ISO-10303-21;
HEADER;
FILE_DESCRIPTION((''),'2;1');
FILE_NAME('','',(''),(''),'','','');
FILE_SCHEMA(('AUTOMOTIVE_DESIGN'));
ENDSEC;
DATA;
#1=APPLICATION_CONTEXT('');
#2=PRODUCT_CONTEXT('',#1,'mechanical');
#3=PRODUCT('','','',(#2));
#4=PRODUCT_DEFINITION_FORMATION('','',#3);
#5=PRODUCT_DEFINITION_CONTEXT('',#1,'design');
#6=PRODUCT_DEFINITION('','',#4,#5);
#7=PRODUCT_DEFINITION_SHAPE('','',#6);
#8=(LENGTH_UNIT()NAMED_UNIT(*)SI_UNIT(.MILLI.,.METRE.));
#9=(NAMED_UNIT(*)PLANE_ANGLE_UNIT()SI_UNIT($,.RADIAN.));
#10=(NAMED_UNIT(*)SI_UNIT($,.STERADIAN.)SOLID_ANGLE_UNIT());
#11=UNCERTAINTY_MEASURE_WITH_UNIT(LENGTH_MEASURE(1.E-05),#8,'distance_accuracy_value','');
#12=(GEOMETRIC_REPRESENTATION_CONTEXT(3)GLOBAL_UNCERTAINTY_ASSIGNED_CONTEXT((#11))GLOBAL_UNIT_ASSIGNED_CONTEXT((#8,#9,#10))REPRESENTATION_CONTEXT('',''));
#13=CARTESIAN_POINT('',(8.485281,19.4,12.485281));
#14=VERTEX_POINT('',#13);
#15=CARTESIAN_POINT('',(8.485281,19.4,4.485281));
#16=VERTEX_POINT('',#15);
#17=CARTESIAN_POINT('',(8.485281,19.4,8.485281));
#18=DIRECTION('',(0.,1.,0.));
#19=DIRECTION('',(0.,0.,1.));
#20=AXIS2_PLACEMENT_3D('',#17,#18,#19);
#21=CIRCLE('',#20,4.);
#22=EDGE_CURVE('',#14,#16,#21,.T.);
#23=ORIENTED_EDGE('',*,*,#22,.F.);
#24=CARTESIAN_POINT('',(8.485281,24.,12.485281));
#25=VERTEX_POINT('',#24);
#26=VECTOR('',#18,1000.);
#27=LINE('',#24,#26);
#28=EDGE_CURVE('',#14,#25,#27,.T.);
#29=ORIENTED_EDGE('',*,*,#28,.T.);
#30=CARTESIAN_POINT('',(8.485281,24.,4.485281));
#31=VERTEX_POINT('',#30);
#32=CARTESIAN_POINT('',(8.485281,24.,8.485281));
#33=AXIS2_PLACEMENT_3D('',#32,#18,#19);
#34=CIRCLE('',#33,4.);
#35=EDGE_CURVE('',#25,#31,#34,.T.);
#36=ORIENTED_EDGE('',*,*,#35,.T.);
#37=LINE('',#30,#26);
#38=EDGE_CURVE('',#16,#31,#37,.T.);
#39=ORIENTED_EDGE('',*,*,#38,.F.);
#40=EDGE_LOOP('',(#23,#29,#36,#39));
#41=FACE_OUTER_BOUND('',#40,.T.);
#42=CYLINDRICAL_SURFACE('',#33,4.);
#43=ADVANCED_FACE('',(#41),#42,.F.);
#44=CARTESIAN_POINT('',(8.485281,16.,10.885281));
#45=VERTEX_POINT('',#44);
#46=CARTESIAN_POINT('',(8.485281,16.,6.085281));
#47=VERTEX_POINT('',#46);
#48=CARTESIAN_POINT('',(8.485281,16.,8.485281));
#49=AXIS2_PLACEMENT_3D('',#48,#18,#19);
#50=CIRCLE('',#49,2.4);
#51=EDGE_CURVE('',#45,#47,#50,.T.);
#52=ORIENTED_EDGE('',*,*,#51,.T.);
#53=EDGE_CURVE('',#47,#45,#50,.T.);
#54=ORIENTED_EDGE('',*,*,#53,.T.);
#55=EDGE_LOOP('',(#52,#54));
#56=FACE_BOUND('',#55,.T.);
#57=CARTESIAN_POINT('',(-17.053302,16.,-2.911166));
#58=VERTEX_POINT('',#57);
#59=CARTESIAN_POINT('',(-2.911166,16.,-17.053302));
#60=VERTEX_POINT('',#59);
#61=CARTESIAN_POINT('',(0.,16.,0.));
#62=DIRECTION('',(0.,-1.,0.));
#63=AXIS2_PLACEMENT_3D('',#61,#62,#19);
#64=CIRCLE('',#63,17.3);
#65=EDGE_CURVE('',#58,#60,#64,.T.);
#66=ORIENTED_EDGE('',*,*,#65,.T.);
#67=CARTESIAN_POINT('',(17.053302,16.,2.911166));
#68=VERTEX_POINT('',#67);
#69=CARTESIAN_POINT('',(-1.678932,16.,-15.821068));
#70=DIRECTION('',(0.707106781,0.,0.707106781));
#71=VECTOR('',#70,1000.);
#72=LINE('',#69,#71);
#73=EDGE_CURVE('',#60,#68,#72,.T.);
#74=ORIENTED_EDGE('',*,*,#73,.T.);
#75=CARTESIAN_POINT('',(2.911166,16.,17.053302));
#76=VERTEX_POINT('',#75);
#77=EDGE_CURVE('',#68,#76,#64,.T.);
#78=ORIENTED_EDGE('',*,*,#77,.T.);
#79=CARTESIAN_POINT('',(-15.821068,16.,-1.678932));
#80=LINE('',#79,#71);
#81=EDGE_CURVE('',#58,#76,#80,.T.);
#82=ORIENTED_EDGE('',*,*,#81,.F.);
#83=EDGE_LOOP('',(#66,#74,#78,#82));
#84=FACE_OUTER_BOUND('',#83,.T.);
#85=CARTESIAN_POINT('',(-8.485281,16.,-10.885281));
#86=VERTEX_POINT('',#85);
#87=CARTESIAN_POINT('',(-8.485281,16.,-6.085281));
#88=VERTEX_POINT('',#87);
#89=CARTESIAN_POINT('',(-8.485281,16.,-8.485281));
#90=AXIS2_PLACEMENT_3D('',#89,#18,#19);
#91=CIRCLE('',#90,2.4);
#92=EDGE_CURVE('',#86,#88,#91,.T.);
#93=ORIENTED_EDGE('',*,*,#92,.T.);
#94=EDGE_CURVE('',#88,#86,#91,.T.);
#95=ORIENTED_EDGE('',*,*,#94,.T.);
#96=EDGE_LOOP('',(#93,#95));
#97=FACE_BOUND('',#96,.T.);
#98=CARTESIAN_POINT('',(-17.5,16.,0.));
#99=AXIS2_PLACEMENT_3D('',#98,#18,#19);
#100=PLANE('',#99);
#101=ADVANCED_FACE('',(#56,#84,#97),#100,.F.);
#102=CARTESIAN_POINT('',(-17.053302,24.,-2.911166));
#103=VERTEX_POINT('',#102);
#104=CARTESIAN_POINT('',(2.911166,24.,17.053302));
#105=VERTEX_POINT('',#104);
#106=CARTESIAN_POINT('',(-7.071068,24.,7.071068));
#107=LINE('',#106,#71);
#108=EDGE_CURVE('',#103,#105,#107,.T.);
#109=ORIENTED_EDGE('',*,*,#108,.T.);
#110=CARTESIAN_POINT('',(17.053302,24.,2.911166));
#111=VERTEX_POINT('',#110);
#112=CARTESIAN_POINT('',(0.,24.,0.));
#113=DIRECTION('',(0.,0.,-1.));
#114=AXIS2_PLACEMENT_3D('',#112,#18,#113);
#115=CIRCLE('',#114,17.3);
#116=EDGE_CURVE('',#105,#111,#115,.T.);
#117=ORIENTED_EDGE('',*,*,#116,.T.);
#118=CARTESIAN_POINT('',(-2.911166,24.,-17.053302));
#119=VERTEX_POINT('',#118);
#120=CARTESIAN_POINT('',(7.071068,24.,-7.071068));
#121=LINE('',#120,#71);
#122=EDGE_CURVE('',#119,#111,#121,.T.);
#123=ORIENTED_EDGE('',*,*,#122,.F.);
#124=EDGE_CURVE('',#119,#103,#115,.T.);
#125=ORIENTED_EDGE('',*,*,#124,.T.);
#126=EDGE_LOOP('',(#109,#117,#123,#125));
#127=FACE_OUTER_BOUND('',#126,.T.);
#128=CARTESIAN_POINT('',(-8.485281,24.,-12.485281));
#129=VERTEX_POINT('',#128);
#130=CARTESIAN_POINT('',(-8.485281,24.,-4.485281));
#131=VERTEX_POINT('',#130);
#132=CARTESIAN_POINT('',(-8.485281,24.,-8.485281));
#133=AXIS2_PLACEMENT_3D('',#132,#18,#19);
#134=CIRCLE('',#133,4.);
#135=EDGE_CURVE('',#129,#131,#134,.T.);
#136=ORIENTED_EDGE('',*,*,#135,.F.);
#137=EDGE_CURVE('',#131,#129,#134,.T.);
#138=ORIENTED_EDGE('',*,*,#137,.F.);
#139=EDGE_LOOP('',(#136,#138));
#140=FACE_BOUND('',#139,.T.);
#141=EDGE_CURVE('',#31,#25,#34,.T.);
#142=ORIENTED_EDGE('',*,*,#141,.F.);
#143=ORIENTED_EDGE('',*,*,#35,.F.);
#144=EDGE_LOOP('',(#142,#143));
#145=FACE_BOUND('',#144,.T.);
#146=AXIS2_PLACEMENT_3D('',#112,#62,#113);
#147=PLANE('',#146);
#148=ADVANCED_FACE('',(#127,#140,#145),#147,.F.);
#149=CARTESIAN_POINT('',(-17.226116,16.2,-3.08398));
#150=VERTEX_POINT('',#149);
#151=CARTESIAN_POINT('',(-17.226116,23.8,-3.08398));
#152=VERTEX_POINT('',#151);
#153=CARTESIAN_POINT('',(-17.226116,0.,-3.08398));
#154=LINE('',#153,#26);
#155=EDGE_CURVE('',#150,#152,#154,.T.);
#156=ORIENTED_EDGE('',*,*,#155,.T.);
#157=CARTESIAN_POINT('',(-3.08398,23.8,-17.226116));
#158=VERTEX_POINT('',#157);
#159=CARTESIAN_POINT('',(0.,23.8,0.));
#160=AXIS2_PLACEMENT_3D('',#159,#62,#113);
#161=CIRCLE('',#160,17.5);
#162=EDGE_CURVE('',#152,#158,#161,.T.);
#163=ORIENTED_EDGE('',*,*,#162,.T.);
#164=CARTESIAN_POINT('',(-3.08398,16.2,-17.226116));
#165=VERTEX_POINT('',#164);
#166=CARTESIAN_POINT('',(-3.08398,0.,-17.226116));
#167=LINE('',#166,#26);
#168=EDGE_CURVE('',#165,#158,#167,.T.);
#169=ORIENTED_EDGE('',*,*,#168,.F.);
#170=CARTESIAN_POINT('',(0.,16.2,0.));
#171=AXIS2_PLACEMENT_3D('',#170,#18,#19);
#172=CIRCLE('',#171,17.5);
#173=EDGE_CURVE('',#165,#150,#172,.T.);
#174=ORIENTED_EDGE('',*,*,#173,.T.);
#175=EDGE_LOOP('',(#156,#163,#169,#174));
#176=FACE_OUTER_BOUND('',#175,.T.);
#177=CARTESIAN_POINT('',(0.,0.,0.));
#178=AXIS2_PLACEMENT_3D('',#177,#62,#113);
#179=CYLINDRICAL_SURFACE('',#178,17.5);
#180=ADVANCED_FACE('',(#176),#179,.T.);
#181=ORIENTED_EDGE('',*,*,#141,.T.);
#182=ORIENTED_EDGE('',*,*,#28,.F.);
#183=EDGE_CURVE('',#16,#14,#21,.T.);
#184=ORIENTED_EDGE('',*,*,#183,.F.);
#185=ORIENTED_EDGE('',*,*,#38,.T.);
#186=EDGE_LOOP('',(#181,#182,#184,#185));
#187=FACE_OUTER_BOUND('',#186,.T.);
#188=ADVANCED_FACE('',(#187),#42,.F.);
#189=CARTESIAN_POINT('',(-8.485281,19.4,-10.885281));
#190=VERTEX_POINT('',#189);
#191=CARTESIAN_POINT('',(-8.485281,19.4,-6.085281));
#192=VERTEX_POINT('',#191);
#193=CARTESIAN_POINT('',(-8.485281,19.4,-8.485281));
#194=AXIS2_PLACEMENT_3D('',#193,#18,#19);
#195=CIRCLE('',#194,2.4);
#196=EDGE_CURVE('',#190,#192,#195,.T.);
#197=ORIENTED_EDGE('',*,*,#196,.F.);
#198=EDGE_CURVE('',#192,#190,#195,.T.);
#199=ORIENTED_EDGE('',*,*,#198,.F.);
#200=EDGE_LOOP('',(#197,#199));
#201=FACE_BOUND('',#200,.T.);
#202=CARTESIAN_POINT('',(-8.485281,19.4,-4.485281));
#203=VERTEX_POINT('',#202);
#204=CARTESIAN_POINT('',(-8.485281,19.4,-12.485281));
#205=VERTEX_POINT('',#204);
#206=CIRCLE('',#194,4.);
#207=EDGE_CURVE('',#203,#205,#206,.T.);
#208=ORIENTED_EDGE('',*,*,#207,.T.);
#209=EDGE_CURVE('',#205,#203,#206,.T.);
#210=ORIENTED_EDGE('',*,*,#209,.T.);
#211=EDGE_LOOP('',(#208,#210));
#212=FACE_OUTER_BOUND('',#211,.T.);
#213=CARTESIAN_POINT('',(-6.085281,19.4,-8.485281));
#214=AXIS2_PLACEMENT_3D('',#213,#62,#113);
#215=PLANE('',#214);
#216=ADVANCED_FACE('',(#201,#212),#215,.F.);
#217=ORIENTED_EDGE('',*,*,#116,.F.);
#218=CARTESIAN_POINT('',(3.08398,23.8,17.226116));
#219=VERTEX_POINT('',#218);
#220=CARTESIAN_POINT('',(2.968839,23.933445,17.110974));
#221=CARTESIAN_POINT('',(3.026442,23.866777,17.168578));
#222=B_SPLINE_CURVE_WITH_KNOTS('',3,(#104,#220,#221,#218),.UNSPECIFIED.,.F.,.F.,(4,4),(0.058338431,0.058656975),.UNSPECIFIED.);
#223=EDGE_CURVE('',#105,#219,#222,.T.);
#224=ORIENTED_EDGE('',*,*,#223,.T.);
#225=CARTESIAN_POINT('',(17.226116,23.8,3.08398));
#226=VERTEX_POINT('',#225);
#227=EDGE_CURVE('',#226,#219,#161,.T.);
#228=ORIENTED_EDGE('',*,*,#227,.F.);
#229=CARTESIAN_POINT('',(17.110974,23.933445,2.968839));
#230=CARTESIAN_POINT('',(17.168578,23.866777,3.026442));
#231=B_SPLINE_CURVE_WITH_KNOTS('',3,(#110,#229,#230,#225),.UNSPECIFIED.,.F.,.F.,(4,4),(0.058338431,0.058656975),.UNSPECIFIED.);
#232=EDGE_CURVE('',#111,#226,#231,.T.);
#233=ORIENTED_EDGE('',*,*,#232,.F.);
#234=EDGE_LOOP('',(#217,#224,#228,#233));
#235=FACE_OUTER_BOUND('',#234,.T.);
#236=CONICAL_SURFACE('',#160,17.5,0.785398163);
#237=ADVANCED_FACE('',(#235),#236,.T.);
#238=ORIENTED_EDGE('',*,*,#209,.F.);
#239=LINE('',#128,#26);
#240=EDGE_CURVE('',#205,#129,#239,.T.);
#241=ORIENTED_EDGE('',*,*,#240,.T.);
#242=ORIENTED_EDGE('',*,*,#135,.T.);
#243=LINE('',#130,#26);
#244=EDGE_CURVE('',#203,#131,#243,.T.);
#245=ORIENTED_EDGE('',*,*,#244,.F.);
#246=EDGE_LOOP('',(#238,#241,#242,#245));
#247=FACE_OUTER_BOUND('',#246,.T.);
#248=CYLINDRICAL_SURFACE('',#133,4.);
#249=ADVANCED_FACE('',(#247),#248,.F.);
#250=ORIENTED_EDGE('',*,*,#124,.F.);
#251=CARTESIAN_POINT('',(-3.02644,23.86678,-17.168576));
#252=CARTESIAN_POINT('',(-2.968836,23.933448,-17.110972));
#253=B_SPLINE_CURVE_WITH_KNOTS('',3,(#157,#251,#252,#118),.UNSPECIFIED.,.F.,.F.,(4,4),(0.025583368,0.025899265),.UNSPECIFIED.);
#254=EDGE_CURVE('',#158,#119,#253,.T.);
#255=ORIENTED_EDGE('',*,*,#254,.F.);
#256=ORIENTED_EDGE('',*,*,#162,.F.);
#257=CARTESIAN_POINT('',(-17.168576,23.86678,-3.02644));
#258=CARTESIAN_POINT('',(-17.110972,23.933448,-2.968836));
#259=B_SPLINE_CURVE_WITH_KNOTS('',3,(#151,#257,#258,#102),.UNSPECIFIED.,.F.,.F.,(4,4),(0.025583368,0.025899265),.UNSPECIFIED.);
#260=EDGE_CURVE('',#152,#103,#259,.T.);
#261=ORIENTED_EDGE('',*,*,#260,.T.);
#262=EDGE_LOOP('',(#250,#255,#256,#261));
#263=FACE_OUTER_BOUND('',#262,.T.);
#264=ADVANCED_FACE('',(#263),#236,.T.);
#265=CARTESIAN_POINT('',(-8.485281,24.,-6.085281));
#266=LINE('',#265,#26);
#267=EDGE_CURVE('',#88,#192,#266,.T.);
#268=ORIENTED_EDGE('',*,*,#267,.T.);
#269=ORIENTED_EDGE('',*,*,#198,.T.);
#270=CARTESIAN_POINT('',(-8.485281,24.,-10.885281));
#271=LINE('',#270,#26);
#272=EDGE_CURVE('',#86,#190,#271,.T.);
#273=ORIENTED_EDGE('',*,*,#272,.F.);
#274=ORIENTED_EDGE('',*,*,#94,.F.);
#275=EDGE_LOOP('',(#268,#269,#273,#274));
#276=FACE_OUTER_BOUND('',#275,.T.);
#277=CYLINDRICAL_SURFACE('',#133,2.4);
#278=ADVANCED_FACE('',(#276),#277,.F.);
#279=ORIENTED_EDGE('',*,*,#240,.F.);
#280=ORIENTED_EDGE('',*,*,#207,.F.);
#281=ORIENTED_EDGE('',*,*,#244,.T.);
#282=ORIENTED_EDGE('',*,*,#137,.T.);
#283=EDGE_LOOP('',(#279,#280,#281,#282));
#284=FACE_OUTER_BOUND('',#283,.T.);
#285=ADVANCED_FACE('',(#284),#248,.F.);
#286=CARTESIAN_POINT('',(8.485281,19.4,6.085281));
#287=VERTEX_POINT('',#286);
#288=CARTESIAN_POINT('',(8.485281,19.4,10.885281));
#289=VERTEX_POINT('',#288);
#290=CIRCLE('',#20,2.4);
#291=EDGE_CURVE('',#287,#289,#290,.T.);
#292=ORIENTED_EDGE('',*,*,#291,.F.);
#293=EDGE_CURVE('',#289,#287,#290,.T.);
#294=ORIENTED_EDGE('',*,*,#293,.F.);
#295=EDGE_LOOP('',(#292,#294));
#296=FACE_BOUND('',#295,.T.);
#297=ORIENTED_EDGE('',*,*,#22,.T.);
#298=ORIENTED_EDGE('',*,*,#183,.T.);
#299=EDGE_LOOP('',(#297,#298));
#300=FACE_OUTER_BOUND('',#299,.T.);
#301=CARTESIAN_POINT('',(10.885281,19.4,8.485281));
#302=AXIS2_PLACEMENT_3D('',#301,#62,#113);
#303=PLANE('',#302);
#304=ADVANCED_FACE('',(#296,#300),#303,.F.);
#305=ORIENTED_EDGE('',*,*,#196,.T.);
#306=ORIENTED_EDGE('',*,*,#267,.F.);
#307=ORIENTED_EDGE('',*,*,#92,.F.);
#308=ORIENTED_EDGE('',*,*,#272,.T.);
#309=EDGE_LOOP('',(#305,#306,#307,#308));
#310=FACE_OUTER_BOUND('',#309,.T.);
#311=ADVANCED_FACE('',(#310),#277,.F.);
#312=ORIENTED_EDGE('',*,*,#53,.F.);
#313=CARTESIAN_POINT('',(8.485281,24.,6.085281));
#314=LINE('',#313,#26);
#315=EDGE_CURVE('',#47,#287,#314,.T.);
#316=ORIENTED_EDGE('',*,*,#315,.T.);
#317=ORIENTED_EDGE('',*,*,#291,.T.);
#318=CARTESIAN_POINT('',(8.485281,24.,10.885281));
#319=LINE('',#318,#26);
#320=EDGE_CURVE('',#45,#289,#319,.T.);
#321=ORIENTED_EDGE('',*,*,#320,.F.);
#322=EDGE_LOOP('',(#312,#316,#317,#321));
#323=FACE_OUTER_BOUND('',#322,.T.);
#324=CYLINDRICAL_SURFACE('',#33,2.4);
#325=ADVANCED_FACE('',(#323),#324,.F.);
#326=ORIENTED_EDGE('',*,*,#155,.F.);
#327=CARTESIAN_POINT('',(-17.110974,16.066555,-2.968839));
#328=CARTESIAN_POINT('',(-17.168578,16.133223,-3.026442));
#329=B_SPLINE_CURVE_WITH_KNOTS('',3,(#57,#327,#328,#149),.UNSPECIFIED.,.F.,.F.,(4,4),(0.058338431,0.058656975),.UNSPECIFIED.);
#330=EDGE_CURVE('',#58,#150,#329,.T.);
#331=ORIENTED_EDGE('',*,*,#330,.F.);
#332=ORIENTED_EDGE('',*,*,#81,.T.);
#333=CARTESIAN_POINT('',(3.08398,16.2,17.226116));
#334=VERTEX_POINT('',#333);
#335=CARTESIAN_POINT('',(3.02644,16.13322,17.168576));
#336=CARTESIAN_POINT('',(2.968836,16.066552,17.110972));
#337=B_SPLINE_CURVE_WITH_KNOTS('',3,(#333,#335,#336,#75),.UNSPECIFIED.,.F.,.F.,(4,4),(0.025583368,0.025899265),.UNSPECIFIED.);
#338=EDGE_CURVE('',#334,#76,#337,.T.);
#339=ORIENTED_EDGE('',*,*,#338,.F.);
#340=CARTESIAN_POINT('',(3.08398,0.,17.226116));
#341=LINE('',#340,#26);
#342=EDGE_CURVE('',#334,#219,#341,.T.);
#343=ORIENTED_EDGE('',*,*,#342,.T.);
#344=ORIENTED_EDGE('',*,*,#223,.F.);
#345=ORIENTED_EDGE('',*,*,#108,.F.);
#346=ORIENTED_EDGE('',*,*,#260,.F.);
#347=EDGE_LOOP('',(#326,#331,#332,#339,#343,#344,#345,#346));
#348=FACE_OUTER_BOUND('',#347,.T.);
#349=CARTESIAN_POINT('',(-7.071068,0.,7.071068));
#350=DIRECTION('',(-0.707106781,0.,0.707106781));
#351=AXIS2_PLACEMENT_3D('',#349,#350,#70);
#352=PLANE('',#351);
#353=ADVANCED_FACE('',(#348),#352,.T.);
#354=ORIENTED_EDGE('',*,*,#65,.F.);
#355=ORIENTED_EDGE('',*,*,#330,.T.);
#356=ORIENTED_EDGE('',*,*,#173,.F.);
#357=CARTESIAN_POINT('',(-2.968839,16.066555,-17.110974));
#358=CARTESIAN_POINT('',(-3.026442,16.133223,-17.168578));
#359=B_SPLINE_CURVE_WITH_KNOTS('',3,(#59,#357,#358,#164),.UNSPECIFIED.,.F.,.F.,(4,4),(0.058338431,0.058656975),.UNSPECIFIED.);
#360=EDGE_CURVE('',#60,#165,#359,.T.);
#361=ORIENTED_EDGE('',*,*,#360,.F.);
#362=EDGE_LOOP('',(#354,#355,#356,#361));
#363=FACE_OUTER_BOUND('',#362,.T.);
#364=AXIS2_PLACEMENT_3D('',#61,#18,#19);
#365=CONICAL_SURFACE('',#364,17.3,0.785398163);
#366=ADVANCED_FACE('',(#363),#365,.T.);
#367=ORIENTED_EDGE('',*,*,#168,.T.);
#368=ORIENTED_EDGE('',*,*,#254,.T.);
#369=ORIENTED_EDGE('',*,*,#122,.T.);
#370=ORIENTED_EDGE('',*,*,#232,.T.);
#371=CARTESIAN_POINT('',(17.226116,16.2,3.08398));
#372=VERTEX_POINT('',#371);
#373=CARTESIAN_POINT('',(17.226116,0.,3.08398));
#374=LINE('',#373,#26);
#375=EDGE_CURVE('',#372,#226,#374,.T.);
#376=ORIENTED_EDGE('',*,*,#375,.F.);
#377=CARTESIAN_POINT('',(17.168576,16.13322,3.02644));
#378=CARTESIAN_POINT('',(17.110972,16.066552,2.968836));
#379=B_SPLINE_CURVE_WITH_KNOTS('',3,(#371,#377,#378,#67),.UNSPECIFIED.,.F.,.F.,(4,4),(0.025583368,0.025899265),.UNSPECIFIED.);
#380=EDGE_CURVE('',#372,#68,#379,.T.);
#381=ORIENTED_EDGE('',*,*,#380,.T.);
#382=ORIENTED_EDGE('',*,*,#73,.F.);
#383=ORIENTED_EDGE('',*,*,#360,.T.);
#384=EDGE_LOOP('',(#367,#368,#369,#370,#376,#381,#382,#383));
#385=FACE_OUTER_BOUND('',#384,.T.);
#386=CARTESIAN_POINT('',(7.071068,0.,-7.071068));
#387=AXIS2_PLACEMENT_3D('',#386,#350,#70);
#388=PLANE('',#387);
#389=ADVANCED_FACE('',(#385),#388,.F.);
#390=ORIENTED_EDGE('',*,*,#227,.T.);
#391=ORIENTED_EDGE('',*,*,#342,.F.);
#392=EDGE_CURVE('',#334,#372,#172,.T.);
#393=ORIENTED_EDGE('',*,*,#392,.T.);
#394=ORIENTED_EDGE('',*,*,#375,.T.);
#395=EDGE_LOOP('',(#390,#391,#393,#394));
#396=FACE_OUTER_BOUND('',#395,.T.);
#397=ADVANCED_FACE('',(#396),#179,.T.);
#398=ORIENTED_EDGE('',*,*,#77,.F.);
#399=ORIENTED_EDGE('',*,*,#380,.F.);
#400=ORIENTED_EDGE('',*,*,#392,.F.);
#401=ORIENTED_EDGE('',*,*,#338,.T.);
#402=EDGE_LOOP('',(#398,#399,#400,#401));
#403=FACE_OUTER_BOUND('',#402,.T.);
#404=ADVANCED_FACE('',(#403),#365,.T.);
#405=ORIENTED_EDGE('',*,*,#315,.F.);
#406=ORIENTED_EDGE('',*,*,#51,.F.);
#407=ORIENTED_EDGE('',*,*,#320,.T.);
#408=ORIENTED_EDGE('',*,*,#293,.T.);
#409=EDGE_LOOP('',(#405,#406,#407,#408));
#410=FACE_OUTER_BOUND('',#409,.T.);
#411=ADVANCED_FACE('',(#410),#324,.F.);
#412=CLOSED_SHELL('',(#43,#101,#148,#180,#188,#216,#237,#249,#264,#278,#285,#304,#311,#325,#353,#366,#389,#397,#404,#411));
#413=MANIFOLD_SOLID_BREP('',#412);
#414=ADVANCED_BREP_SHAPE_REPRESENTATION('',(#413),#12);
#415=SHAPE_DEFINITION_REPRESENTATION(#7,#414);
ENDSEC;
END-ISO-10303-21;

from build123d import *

# Parameters (mm, degrees)
G1_8_TAPPED_HOLE1_D                               = 8.8
HOLE_SIZE_BASED_ON_SOCKET_HEAD_CAP_SC_D           = 4.8
HOLE_SIZE_BASED_ON_SOCKET_HEAD_CAP_SC_CBORE_D     = 8
HOLE_SIZE_BASED_ON_SOCKET_HEAD_CAP_SC_CBORE_DEPTH = 4.6
FILLET1_R                                         = 0.2
CHAMFER1_SIZE                                     = 0.2
CHAMFER2_SIZE                                     = 0.5
CUT_EXTRUDE1_DEPTH                                = 35.474628352
SKETCH8_R                                         = 15
CUT_EXTRUDE2_DEPTH                                = 30.145808143
SKETCH9_R                                         = 7
BOSS_EXTRUDE1_DEPTH                               = 8


with BuildPart() as part:
    # Sketch2 → Revolve1 (revolve)
    with BuildSketch(Plane.XY, mode=Mode.PRIVATE) as revolve1_sk:
        Polygon((0, 24), (-17.5, 24), (-17.5, 16), (-6.75, 16), (-6.75, 0), (0, 0), align=None)
    revolve(revolve1_sk.sketch.rotate(Axis((0, 0, 0), (0, 1, 0)), 270), axis=Axis((0, 0, 0), (0, 1, 0)))

    # G1/8 Tapped Hole1 (through all)
    with Locations(Plane.ZX.offset(24)):
        with Locations((0, 0)):
            Hole(G1_8_TAPPED_HOLE1_D / 2)

    # Hole Size (% based on) Socket Head Cap Screw Type 1 (through all)
    with Locations(Plane(origin=(-8.485281374, 24, -8.485281374), x_dir=(0, 0, 1), z_dir=(0, 1, 0))):
        with Locations((0, 0), (16.970562748, 16.970562748)):
            CounterBoreHole(HOLE_SIZE_BASED_ON_SOCKET_HEAD_CAP_SC_D / 2, HOLE_SIZE_BASED_ON_SOCKET_HEAD_CAP_SC_CBORE_D / 2, HOLE_SIZE_BASED_ON_SOCKET_HEAD_CAP_SC_CBORE_DEPTH)

    # Fillet1
    fillet1_edges = [part.edges().sort_by_distance(p)[0] for p in [
        (0, 16, 6.75),
    ]]
    fillet(fillet1_edges, radius=FILLET1_R)

    # Chamfer1
    chamfer1_edges = [part.edges().sort_by_distance(p)[0] for p in [
        (0, 0, 6.75),
        (0, 16, 17.5),
        (0, 24, 17.5),
    ]]
    chamfer(chamfer1_edges, length=CHAMFER1_SIZE)

    # Chamfer2
    chamfer2_edges = [part.edges().sort_by_distance(p)[0] for p in [
        (0, 24, 4.4),
        (0, 0, 4.4),
    ]]
    chamfer(chamfer2_edges, length=CHAMFER2_SIZE)

    # Sketch7 → Cut-Extrude1 (cut, through all)
    with BuildSketch(Plane(origin=(0, 24, 0), x_dir=(1, 0, 0), z_dir=(0, 1, 0))):
        with BuildLine():
            Line((2.911166407, -17.053302031), (-17.053302031, 2.911166407))
            ThreePointArc((-17.053302031, 2.911166407), (-12.232947315, -12.232947315), (2.911166407, -17.053302031))
        make_face()
        with BuildLine():
            ThreePointArc((17.3, 0), (11.156317071, 13.222200627), (-2.911166407, 17.053302031))
            Line((-2.911166407, 17.053302031), (17.053302031, -2.911166407))
            ThreePointArc((17.053302031, -2.911166407), (17.238215179, -1.460800272), (17.3, 0))
        make_face()
        with BuildLine():
            Line((-17.053302031, 2.911166407), (-17.226115818, 3.083980194))
            ThreePointArc((-17.226115818, 3.083980194), (-12.374368671, -12.374368671), (3.083980194, -17.226115818))
            Line((3.083980194, -17.226115818), (2.911166407, -17.053302031))
            ThreePointArc((2.911166407, -17.053302031), (-12.232947315, -12.232947315), (-17.053302031, 2.911166407))
        make_face()
        with BuildLine():
            ThreePointArc((17.5, 0), (11.23121424, 13.42050024), (-3.083980194, 17.226115818))
            Line((-3.083980194, 17.226115818), (-2.911166407, 17.053302031))
            ThreePointArc((-2.911166407, 17.053302031), (11.156317071, 13.222200627), (17.3, 0))
            ThreePointArc((17.3, 0), (17.238215179, -1.460800272), (17.053302031, -2.911166407))
            Line((17.053302031, -2.911166407), (17.226115818, -3.083980194))
            ThreePointArc((17.226115818, -3.083980194), (17.431394477, -1.548058977), (17.5, 0))
        make_face()
    extrude(amount=-CUT_EXTRUDE1_DEPTH, mode=Mode.SUBTRACT)

    # Sketch8 → Cut-Extrude2 (cut, through all)
    with BuildSketch(Plane.XZ.offset(-16)):
        Circle(SKETCH8_R)
    extrude(amount=CUT_EXTRUDE2_DEPTH, mode=Mode.SUBTRACT)

    # Sketch9 → Boss-Extrude1 (add)
    with BuildSketch(Plane.XZ.offset(-16)):
        Circle(SKETCH9_R)
    extrude(amount=-BOSS_EXTRUDE1_DEPTH)


solid = part.part
